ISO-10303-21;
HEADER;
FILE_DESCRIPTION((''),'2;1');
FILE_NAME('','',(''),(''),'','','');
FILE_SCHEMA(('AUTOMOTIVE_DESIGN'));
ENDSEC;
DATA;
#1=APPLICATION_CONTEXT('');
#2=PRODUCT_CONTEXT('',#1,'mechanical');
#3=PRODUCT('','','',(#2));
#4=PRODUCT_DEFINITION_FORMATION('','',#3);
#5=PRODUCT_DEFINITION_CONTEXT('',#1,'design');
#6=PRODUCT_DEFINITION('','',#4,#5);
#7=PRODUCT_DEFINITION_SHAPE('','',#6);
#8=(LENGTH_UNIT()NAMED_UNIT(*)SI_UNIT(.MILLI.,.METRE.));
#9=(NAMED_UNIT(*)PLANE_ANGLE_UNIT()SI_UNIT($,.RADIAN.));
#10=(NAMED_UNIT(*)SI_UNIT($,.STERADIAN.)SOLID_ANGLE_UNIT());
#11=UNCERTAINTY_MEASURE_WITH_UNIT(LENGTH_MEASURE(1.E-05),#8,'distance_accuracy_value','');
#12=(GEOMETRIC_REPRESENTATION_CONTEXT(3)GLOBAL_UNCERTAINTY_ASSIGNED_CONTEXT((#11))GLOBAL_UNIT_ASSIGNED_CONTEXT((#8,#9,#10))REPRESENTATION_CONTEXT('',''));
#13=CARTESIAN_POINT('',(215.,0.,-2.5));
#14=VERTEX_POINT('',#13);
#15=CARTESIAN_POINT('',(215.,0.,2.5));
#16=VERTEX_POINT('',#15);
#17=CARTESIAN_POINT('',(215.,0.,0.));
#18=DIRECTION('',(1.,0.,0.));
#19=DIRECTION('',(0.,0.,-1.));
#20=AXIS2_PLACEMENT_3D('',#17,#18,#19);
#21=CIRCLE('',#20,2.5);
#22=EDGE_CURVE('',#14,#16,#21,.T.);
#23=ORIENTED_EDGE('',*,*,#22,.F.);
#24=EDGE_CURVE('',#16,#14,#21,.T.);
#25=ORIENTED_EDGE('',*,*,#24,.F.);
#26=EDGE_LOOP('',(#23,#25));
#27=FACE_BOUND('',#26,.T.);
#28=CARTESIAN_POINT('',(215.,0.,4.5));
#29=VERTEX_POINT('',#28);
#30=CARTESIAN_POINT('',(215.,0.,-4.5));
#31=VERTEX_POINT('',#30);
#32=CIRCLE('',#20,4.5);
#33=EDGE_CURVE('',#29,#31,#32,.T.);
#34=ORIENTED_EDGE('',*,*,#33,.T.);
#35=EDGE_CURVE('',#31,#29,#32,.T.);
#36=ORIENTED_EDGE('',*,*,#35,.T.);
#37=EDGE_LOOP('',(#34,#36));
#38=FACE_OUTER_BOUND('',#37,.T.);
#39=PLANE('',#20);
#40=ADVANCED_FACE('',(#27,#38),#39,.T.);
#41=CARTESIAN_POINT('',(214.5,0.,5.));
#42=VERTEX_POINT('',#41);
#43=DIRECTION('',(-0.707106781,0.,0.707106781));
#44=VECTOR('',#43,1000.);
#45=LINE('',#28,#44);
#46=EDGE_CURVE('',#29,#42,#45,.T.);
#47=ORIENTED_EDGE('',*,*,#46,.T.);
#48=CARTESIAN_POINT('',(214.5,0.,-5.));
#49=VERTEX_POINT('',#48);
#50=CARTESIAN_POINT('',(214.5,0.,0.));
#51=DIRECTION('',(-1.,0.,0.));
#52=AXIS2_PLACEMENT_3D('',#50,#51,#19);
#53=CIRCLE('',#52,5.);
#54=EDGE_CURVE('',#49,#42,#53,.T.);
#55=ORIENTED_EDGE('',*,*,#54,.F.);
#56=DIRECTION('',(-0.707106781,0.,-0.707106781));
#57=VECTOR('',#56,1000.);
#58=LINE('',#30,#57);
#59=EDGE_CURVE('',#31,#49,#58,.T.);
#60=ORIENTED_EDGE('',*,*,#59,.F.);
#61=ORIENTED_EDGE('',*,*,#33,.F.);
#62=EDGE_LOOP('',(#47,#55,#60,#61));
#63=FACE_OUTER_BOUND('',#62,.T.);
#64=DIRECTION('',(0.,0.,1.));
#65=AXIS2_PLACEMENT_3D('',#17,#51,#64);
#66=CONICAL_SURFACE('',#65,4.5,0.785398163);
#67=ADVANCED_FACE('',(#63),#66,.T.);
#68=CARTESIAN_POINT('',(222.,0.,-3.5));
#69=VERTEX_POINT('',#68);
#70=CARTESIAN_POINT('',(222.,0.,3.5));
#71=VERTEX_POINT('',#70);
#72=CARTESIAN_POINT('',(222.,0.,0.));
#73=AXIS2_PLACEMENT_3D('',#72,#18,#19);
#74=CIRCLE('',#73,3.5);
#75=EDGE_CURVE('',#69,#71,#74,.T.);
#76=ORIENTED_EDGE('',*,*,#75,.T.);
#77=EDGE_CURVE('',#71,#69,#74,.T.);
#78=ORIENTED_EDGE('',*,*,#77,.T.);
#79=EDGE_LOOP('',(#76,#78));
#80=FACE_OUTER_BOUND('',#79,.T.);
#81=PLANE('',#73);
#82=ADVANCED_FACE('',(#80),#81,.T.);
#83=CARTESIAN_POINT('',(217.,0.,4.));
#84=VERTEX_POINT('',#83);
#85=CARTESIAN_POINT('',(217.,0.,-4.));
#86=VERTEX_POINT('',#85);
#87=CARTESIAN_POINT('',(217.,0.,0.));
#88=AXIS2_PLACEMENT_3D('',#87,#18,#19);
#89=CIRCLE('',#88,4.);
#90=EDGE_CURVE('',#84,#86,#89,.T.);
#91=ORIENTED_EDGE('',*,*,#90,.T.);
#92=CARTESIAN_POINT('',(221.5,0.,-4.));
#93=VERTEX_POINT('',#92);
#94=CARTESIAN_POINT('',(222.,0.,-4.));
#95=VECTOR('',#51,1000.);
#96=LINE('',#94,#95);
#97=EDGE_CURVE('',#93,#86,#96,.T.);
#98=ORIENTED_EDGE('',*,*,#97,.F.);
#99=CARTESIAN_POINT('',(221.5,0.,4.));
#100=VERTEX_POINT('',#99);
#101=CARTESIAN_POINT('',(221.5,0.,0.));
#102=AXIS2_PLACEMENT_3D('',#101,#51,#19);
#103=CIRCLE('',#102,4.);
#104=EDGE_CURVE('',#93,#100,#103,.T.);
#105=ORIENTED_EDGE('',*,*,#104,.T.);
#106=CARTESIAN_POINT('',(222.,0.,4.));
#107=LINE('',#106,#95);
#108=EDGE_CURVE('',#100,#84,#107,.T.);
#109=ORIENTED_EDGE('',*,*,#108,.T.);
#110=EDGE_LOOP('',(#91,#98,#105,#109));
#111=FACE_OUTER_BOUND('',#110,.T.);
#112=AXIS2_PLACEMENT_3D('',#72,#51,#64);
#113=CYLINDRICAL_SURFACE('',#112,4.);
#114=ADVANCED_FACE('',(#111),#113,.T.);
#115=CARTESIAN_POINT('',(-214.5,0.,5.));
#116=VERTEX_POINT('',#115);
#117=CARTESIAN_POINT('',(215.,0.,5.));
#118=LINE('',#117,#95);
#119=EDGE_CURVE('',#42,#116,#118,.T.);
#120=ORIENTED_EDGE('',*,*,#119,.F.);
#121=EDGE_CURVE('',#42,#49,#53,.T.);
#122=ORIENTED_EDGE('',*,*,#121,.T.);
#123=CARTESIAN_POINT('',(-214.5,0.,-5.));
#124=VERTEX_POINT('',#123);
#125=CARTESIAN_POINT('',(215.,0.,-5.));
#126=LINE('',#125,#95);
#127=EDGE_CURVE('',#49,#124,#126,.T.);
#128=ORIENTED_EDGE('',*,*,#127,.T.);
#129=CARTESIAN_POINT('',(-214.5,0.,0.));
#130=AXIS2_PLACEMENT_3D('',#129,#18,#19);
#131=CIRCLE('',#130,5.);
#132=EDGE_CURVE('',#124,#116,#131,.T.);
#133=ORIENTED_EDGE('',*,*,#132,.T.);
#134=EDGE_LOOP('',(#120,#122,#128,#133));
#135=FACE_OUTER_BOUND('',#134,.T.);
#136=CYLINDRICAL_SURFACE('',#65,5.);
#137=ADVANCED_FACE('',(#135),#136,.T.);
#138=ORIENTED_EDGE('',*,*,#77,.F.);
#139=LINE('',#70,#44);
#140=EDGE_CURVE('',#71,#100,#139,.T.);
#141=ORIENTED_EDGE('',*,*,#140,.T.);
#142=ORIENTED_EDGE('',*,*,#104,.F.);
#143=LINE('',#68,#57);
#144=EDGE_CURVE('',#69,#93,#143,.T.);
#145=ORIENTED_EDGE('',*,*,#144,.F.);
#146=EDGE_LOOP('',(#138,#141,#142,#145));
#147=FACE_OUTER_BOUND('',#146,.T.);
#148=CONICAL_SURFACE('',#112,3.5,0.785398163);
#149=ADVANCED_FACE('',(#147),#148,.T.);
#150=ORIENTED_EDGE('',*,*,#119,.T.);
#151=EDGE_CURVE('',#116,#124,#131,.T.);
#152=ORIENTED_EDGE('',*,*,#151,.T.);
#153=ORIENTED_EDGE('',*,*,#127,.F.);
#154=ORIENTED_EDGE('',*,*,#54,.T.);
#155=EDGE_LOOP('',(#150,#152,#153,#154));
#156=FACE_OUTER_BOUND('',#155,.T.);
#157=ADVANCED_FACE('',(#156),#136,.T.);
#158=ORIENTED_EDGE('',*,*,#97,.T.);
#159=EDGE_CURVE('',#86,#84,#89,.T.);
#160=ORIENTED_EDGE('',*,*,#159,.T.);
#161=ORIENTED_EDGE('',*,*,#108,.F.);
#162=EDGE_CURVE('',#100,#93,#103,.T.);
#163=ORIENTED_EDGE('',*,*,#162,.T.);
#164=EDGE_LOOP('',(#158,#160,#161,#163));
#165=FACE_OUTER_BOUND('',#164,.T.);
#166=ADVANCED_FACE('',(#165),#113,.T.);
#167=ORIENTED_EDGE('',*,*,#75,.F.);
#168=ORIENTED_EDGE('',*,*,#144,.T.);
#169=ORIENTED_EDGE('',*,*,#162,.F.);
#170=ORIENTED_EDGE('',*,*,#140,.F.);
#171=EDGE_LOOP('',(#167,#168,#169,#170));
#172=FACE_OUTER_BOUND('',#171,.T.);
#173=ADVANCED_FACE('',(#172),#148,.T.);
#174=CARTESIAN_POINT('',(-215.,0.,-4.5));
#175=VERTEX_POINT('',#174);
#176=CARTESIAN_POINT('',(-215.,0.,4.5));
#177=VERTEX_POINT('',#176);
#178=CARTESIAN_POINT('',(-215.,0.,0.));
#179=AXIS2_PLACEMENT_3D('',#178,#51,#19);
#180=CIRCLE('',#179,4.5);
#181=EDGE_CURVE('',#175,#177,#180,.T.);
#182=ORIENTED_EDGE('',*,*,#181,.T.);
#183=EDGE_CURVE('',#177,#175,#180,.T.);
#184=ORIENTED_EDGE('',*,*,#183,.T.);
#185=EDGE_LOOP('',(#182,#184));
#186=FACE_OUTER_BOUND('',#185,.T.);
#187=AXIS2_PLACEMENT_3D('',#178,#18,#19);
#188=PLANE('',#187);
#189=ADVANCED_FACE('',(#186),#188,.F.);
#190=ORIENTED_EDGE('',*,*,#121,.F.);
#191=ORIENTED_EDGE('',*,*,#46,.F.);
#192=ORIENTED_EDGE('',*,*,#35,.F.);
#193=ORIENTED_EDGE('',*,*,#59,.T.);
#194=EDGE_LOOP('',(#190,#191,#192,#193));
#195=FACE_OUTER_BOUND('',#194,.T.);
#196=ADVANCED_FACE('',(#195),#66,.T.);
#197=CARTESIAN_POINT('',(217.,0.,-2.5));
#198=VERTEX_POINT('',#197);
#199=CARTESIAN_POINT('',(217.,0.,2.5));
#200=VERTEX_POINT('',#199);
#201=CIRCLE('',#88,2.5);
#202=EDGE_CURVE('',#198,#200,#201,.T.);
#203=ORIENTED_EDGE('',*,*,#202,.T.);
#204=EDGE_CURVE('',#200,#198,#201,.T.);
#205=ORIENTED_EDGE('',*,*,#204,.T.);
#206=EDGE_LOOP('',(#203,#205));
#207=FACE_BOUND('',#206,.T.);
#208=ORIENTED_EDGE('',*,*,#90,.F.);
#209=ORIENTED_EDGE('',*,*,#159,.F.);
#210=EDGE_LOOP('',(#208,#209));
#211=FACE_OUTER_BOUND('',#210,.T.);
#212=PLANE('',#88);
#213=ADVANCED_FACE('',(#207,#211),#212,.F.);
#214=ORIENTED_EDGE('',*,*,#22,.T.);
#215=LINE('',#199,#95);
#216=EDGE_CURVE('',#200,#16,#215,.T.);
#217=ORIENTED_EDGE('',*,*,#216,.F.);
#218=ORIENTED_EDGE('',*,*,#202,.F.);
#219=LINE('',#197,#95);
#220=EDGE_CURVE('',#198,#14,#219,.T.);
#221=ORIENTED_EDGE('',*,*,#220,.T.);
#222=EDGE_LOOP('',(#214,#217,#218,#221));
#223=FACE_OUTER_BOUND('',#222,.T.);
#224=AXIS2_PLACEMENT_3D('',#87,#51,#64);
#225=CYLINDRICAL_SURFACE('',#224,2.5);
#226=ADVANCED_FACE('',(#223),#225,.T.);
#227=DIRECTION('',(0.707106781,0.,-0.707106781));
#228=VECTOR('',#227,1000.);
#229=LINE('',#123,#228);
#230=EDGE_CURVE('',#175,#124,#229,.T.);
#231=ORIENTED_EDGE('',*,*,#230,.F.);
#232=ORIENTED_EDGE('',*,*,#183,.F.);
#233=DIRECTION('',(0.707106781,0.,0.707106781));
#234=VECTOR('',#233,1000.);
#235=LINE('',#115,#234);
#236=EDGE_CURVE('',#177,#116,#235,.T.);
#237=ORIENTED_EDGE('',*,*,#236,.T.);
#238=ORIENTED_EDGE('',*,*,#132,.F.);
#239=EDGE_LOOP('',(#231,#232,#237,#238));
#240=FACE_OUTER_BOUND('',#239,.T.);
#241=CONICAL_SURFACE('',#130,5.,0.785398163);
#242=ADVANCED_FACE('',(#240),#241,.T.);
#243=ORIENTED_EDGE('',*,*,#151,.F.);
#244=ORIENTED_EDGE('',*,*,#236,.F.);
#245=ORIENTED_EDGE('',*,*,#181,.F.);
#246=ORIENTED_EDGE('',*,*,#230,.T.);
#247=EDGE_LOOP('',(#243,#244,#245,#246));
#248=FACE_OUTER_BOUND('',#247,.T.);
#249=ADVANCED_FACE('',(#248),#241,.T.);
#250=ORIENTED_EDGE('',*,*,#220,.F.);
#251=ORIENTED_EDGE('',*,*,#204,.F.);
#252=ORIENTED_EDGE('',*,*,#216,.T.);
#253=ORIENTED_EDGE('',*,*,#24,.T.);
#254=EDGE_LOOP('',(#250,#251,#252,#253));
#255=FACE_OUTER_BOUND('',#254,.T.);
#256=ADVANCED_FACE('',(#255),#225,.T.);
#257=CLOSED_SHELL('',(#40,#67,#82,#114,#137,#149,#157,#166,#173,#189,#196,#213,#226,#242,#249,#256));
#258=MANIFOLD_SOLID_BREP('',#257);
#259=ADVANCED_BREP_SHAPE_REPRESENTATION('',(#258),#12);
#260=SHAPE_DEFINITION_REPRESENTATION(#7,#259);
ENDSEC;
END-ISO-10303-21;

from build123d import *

# Parameters (mm, degrees)
SKETCH1_R           = 5
BOSS_EXTRUDE1_DEPTH = 215
SKETCH2_R           = 2.5
BOSS_EXTRUDE2_DEPTH = 2
SKETCH3_R           = 4
BOSS_EXTRUDE3_DEPTH = 5
CHAMFER1_SIZE       = 0.5


with BuildPart() as part:
    # Sketch1 → Boss-Extrude1 (new, symmetric)
    with BuildSketch(Plane(origin=(0, 0, 0), x_dir=(0, 0, -1), z_dir=(1, 0, 0))):
        Circle(SKETCH1_R)
    extrude(amount=BOSS_EXTRUDE1_DEPTH, both=True)

    # Sketch2 → Boss-Extrude2 (add)
    with BuildSketch(Plane(origin=(215, 0, 0), x_dir=(0, 0, -1), z_dir=(1, 0, 0))):
        Circle(SKETCH2_R)
    extrude(amount=BOSS_EXTRUDE2_DEPTH)

    # Sketch3 → Boss-Extrude3 (add)
    with BuildSketch(Plane(origin=(217, 0, 0), x_dir=(0, 0, -1), z_dir=(1, 0, 0))):
        Circle(SKETCH3_R)
    extrude(amount=BOSS_EXTRUDE3_DEPTH)

    # Chamfer1
    chamfer1_edges = [part.edges().sort_by_distance(p)[0] for p in [
        (-215, 0, 5),
        (215, 0, 5),
        (222, 0, 4),
    ]]
    chamfer(chamfer1_edges, length=CHAMFER1_SIZE)


solid = part.part
